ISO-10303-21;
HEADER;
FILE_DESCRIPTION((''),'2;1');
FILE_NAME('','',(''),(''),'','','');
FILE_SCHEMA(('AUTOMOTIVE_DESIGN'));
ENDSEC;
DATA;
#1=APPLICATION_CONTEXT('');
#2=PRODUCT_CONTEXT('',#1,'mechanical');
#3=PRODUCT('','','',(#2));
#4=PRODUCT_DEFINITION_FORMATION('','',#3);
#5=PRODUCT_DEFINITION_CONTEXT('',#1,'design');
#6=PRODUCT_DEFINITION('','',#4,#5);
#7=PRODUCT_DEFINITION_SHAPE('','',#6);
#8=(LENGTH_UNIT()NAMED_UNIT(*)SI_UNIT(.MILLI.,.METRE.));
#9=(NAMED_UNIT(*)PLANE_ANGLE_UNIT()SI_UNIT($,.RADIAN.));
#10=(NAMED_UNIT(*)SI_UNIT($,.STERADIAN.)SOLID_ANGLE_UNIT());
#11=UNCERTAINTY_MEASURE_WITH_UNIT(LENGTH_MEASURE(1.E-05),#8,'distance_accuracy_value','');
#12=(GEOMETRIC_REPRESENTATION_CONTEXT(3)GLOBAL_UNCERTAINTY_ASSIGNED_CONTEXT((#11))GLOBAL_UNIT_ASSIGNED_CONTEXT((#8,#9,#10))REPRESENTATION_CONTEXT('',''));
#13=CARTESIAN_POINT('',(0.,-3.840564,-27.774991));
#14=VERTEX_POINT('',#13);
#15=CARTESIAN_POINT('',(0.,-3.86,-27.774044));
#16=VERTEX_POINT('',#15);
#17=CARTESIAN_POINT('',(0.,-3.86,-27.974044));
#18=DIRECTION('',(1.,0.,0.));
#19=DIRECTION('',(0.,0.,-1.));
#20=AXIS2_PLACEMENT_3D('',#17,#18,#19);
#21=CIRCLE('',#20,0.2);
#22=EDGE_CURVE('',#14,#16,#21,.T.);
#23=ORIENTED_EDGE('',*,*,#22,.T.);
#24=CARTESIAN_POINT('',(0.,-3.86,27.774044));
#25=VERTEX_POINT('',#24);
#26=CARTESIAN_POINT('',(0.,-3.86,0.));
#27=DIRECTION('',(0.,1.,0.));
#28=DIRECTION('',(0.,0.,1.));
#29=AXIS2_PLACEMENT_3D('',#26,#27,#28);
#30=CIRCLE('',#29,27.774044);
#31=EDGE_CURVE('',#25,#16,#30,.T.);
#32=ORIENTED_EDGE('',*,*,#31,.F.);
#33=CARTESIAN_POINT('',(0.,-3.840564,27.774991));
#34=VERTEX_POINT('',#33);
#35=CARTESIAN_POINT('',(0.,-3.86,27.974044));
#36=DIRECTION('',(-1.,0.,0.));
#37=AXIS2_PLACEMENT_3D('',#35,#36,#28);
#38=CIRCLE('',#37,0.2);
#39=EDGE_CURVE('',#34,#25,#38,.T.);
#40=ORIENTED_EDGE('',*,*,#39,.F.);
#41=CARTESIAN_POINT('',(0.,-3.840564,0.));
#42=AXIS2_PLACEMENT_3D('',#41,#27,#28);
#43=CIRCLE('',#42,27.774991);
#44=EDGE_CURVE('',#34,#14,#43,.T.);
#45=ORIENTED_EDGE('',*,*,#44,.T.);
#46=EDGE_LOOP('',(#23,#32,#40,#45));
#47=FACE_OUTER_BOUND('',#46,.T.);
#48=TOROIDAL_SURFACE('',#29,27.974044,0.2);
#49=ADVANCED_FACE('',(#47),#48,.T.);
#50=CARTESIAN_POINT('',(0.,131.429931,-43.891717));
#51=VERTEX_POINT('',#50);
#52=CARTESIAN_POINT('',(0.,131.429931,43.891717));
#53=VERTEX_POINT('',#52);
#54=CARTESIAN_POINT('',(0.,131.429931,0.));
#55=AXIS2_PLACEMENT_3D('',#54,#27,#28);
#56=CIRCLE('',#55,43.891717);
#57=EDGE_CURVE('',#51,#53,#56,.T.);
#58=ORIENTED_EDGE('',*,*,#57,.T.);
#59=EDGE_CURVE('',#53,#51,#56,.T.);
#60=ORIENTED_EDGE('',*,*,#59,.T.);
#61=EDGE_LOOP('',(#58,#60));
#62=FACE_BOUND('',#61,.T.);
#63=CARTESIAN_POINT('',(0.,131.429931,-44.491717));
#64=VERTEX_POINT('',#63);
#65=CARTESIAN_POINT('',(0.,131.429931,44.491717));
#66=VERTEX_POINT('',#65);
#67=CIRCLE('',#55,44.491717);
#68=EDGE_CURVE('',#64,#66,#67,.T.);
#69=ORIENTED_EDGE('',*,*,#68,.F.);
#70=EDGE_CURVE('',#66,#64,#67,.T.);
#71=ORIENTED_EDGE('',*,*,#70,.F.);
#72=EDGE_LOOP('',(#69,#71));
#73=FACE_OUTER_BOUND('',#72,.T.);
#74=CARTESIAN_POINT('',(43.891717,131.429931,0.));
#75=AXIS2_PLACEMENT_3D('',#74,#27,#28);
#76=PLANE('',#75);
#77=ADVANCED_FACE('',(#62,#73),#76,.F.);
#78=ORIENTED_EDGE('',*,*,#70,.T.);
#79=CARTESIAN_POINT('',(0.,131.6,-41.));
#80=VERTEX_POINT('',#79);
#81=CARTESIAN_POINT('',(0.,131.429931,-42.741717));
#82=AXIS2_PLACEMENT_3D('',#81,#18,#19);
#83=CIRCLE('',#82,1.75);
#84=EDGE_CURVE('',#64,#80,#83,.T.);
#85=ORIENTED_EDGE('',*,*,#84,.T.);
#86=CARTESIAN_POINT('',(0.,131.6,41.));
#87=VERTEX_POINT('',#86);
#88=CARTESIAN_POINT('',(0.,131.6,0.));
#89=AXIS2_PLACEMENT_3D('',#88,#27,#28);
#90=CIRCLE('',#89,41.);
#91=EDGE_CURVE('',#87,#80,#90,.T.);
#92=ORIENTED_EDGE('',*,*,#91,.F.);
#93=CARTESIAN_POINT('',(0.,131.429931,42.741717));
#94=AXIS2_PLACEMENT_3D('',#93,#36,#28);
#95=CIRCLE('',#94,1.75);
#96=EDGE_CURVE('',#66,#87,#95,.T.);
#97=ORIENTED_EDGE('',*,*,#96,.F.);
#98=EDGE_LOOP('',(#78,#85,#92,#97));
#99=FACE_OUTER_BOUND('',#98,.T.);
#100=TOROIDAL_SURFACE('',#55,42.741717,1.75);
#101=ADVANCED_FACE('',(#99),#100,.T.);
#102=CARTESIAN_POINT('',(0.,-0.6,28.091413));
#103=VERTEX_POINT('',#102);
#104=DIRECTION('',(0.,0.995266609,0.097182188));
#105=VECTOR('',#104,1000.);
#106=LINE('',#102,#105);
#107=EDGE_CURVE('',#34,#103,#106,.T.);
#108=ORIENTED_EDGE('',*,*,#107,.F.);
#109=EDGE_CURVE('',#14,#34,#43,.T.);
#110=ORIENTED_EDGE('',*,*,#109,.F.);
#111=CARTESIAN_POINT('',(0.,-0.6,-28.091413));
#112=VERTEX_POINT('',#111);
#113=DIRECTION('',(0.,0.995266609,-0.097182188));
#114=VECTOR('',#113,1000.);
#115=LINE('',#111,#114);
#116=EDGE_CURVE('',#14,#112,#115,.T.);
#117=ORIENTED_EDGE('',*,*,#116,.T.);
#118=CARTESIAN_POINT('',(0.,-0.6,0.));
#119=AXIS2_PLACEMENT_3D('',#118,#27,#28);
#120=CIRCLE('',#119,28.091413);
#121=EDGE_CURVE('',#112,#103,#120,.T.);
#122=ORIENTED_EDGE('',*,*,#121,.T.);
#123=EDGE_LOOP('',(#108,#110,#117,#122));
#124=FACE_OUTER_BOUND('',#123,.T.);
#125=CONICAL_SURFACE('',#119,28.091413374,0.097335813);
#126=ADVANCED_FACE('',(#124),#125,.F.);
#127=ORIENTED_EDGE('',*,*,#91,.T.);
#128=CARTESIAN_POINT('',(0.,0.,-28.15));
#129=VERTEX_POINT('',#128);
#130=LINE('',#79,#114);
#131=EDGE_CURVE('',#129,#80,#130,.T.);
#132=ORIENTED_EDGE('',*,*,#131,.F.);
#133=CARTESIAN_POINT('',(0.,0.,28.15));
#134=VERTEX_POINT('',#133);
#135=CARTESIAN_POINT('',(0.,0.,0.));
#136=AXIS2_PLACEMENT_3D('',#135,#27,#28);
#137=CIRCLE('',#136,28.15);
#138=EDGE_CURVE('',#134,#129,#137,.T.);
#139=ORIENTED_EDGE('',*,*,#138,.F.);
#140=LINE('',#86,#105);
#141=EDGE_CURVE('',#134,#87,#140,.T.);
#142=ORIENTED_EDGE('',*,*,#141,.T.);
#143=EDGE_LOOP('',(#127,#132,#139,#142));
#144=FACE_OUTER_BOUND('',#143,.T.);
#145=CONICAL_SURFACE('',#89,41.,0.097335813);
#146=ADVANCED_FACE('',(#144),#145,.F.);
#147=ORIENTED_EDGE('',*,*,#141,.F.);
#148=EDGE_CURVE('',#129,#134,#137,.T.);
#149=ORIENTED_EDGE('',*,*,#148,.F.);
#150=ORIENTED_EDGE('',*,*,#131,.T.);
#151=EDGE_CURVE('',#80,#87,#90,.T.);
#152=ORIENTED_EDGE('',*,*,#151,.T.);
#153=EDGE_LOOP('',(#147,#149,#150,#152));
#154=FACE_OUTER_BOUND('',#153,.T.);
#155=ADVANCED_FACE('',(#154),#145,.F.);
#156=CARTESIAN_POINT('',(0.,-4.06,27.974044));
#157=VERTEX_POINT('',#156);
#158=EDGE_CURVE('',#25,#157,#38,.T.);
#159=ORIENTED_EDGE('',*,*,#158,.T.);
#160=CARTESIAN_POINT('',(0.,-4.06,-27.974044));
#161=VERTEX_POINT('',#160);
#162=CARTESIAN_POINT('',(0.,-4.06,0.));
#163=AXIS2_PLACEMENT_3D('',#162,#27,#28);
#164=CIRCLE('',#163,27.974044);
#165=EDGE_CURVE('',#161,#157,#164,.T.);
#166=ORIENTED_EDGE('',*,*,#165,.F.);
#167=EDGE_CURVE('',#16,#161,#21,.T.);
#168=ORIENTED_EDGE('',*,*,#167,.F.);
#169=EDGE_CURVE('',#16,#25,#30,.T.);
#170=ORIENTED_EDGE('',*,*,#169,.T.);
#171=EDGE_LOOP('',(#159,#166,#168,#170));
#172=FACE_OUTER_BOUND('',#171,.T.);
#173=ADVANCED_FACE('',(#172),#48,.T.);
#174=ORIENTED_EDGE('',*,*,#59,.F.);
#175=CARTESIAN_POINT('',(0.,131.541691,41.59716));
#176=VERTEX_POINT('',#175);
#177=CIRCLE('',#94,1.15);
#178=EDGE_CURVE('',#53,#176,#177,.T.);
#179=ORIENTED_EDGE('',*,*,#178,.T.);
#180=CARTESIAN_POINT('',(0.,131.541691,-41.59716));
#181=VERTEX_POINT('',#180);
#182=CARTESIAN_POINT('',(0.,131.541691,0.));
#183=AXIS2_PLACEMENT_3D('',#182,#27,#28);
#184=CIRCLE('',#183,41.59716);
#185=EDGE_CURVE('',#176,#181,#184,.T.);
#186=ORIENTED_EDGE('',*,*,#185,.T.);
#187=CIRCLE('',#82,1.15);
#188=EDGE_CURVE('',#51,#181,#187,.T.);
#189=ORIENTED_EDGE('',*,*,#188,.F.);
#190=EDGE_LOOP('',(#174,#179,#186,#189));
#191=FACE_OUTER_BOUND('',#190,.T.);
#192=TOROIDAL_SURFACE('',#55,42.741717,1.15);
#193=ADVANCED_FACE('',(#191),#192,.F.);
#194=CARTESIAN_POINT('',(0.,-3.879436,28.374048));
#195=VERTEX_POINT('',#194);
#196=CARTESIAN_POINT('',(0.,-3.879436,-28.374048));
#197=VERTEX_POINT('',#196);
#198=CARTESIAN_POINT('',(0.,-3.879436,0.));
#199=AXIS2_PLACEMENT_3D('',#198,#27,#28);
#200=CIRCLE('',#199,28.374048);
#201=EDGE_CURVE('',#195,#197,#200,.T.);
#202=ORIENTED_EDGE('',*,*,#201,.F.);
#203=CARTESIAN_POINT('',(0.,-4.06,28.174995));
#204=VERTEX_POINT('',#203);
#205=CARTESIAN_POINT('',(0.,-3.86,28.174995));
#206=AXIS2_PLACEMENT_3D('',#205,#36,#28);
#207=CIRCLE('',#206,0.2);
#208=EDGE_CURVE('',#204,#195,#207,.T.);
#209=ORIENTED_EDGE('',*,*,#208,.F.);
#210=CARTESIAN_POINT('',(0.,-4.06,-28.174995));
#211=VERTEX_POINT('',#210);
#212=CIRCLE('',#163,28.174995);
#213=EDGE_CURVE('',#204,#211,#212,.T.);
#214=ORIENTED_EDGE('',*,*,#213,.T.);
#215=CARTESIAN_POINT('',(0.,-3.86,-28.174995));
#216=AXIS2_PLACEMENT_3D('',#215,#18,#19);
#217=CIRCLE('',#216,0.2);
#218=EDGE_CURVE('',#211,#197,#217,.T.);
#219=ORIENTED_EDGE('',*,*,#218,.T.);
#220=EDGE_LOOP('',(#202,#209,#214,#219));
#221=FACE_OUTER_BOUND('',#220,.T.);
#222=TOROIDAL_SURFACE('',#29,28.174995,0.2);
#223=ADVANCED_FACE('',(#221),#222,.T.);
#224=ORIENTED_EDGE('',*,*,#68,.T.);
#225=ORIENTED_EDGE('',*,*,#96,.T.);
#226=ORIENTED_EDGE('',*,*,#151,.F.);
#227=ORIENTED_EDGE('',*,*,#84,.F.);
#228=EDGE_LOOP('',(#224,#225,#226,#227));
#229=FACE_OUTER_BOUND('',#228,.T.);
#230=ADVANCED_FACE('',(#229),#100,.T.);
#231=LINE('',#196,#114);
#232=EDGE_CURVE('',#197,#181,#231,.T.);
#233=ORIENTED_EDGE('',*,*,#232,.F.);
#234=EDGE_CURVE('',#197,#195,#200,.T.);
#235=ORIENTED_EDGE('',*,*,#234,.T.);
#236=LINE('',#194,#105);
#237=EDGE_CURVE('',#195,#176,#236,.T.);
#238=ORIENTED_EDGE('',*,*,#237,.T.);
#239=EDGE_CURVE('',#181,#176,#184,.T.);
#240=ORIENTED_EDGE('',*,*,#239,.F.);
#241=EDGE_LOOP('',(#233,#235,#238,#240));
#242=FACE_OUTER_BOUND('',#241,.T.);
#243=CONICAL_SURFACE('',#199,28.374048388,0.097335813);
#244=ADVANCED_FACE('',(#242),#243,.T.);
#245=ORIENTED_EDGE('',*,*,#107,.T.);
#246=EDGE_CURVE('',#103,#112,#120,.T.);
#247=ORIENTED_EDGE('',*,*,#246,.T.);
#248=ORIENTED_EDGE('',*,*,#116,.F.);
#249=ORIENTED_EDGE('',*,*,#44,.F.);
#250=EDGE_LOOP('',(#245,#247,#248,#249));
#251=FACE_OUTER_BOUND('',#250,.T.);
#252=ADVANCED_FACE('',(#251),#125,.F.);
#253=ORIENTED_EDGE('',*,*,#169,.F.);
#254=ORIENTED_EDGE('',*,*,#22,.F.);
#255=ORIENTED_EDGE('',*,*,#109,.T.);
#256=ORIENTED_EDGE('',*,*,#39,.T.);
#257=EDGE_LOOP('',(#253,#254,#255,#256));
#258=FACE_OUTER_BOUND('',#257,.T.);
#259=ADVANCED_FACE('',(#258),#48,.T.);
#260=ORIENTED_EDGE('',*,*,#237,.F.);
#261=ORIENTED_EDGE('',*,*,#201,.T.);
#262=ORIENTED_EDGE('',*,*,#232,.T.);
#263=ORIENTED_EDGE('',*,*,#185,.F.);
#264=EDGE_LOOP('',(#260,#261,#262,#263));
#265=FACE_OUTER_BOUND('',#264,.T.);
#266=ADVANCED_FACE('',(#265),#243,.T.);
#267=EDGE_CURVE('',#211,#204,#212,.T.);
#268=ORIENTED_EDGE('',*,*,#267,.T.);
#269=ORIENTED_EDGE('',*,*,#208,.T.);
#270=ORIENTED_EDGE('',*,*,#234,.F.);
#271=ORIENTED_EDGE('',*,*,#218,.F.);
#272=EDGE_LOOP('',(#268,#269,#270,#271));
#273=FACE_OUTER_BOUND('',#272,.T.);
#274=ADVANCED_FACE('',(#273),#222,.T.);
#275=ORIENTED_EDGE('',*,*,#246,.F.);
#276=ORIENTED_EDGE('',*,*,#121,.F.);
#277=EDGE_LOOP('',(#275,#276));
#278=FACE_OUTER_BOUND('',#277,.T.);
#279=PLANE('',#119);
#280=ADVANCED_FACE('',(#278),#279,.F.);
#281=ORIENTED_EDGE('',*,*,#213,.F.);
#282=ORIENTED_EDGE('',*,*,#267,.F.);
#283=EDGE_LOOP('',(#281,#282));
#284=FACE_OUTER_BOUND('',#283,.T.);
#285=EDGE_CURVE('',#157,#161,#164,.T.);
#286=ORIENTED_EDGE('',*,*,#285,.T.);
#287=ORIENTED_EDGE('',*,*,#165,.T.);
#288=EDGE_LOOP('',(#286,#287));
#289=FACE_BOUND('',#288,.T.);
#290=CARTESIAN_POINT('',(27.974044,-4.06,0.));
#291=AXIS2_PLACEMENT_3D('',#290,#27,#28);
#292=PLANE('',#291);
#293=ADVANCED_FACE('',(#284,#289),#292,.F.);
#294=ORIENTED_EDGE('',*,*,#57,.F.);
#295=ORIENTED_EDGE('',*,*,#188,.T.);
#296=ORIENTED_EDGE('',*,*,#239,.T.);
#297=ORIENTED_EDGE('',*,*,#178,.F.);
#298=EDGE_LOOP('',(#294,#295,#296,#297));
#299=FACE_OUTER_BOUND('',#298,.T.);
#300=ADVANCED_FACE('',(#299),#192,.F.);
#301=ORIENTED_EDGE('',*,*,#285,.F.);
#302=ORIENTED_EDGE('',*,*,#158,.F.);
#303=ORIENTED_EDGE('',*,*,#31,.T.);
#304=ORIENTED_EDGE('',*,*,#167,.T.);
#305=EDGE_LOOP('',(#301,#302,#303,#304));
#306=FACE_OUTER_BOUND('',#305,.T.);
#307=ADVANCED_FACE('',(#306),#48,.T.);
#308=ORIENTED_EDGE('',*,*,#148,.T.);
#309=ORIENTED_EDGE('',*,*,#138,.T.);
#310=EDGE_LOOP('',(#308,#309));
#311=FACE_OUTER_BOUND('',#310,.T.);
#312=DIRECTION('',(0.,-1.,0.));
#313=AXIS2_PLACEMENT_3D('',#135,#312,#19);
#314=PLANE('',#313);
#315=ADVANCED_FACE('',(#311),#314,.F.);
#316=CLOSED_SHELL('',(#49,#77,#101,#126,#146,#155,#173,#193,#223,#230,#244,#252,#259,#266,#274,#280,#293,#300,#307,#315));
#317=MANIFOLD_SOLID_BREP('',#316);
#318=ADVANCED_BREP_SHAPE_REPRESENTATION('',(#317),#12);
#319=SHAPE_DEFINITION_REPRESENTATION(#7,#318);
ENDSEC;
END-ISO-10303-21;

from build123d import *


with BuildPart() as part:
    # 草图1 → 旋转1 (revolve)
    with BuildSketch(Plane.XY, mode=Mode.PRIVATE) as revolve_1_sk:
        with BuildLine():
            Line((0, 0), (28.15, 0))
            Line((28.15, 0), (41, 131.6))
            ThreePointArc((41, 131.6), (42.826851784, 133.177859086), (44.491716565, 131.429931171))
            Line((44.491716565, 131.429931171), (43.891716565, 131.429931171))
            ThreePointArc((43.891716565, 131.429931171), (42.797662566, 132.578569515), (41.597159965, 131.541690687))
            Line((41.597159965, 131.541690687), (28.374048388, -3.879436438))
            ThreePointArc((28.374048388, -3.879436438), (28.309369008, -4.008133871), (28.174995066, -4.06))
            Line((28.174995066, -4.06), (27.974043886, -4.06))
            ThreePointArc((27.974043886, -4.06), (27.825910015, -3.994373942), (27.774990564, -3.840563562))
            Line((27.774990564, -3.840563562), (28.091413374, -0.6))
            Line((28.091413374, -0.6), (0, -0.6))
            Line((0, -0.6), (0, 0))
        make_face()
    revolve(revolve_1_sk.sketch.rotate(Axis((0, 0, 0), (0, -1, 0)), 90), axis=Axis((0, 0, 0), (0, -1, 0)))


solid = part.part
